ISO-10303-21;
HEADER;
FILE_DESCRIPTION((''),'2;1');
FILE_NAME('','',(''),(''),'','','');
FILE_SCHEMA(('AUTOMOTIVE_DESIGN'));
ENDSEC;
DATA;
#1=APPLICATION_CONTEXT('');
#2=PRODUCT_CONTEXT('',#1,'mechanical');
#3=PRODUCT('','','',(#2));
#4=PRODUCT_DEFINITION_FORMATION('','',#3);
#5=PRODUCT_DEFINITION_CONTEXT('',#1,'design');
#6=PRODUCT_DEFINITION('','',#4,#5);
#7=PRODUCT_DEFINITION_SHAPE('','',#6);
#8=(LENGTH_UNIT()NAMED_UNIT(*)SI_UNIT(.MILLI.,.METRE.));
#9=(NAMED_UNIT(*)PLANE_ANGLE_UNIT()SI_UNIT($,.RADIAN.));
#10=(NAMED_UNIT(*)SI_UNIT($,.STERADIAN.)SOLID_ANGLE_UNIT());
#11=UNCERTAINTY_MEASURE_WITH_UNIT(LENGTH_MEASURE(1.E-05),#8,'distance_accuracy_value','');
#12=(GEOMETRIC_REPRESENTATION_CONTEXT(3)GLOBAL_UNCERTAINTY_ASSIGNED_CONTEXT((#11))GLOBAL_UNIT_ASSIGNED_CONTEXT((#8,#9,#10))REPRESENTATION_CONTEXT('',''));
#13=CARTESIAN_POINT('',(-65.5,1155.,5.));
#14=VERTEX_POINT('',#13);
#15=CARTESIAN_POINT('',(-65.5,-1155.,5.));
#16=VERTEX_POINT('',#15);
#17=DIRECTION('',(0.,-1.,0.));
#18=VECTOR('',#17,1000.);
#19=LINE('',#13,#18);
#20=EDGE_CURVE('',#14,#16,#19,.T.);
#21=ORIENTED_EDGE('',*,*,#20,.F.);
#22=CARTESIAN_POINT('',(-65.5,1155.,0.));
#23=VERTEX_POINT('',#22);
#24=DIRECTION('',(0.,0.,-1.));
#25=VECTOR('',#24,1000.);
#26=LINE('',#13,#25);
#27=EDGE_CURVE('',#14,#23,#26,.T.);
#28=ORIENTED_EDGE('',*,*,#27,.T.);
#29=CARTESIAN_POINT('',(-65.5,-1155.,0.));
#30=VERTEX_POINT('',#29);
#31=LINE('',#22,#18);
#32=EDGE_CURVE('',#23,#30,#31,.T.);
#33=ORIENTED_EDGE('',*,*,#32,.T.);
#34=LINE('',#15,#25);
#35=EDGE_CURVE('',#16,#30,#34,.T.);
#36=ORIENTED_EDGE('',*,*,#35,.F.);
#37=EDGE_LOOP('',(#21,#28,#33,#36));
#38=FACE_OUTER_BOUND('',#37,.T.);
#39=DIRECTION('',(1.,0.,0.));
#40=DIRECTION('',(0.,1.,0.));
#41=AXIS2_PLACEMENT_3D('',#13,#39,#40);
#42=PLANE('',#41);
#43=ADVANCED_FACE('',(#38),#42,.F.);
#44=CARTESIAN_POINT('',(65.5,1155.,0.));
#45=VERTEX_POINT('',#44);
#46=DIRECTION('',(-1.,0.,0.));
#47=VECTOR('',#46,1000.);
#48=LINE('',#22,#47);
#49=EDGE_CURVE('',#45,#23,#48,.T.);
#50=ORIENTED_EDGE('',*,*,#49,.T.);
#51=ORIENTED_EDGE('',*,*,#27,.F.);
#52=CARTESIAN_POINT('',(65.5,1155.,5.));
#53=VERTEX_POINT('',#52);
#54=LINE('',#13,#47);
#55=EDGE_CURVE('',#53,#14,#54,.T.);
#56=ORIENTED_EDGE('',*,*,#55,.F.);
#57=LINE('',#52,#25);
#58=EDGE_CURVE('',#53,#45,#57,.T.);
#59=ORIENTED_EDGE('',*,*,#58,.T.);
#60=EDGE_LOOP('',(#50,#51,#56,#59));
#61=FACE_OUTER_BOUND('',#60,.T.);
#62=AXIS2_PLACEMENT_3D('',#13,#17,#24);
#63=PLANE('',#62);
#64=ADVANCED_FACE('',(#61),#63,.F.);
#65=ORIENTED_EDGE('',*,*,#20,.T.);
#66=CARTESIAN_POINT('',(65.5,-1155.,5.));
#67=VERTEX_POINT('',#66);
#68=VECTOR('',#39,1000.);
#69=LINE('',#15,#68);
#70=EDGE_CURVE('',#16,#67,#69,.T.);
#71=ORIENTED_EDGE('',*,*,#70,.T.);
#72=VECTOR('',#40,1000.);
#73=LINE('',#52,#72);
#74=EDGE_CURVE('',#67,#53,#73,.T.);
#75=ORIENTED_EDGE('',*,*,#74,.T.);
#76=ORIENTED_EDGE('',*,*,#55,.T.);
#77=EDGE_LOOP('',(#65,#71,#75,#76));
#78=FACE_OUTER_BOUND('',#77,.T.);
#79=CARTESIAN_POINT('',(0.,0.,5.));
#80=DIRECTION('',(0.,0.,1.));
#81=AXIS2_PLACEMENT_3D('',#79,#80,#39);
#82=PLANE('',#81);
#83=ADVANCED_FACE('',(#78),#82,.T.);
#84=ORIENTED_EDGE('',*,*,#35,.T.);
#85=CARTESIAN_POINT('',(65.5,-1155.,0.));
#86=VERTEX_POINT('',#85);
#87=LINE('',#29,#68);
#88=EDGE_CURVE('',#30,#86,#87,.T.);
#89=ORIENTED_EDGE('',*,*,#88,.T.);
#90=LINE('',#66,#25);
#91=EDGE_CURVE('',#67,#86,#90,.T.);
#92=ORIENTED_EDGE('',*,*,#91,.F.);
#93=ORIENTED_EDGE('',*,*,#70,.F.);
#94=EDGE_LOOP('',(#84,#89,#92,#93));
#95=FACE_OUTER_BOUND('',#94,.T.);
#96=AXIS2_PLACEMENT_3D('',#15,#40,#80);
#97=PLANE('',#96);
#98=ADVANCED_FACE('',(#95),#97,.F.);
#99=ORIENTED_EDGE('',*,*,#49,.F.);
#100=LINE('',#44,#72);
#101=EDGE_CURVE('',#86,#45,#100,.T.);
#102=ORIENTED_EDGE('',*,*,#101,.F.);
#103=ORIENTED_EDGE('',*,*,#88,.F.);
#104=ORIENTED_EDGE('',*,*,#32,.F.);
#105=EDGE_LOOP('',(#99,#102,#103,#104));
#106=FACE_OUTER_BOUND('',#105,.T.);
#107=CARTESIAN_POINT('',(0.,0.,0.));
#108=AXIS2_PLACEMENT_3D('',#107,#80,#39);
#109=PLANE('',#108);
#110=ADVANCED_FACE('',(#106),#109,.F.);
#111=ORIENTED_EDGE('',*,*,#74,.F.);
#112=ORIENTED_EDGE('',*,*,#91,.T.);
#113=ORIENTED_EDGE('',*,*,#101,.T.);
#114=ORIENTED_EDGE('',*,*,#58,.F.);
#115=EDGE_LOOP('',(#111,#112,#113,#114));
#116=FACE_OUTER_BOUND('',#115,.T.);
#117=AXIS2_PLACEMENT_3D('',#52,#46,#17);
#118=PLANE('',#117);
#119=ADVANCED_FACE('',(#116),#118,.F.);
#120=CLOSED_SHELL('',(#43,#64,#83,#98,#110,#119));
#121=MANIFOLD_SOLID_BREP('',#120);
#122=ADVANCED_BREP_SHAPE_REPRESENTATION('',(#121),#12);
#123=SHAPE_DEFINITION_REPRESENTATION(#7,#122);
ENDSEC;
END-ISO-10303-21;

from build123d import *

# Parameters (mm, degrees)
SKETCH_1_W      = 131
SKETCH_1_H      = 2310
EXTRUDE_1_DEPTH = 5


with BuildPart() as part:
    # 草图1 → 凸台-拉伸1 (new body)
    with BuildSketch(Plane.XY):
        Rectangle(SKETCH_1_W, SKETCH_1_H)
    extrude(amount=EXTRUDE_1_DEPTH)


solid = part.part
